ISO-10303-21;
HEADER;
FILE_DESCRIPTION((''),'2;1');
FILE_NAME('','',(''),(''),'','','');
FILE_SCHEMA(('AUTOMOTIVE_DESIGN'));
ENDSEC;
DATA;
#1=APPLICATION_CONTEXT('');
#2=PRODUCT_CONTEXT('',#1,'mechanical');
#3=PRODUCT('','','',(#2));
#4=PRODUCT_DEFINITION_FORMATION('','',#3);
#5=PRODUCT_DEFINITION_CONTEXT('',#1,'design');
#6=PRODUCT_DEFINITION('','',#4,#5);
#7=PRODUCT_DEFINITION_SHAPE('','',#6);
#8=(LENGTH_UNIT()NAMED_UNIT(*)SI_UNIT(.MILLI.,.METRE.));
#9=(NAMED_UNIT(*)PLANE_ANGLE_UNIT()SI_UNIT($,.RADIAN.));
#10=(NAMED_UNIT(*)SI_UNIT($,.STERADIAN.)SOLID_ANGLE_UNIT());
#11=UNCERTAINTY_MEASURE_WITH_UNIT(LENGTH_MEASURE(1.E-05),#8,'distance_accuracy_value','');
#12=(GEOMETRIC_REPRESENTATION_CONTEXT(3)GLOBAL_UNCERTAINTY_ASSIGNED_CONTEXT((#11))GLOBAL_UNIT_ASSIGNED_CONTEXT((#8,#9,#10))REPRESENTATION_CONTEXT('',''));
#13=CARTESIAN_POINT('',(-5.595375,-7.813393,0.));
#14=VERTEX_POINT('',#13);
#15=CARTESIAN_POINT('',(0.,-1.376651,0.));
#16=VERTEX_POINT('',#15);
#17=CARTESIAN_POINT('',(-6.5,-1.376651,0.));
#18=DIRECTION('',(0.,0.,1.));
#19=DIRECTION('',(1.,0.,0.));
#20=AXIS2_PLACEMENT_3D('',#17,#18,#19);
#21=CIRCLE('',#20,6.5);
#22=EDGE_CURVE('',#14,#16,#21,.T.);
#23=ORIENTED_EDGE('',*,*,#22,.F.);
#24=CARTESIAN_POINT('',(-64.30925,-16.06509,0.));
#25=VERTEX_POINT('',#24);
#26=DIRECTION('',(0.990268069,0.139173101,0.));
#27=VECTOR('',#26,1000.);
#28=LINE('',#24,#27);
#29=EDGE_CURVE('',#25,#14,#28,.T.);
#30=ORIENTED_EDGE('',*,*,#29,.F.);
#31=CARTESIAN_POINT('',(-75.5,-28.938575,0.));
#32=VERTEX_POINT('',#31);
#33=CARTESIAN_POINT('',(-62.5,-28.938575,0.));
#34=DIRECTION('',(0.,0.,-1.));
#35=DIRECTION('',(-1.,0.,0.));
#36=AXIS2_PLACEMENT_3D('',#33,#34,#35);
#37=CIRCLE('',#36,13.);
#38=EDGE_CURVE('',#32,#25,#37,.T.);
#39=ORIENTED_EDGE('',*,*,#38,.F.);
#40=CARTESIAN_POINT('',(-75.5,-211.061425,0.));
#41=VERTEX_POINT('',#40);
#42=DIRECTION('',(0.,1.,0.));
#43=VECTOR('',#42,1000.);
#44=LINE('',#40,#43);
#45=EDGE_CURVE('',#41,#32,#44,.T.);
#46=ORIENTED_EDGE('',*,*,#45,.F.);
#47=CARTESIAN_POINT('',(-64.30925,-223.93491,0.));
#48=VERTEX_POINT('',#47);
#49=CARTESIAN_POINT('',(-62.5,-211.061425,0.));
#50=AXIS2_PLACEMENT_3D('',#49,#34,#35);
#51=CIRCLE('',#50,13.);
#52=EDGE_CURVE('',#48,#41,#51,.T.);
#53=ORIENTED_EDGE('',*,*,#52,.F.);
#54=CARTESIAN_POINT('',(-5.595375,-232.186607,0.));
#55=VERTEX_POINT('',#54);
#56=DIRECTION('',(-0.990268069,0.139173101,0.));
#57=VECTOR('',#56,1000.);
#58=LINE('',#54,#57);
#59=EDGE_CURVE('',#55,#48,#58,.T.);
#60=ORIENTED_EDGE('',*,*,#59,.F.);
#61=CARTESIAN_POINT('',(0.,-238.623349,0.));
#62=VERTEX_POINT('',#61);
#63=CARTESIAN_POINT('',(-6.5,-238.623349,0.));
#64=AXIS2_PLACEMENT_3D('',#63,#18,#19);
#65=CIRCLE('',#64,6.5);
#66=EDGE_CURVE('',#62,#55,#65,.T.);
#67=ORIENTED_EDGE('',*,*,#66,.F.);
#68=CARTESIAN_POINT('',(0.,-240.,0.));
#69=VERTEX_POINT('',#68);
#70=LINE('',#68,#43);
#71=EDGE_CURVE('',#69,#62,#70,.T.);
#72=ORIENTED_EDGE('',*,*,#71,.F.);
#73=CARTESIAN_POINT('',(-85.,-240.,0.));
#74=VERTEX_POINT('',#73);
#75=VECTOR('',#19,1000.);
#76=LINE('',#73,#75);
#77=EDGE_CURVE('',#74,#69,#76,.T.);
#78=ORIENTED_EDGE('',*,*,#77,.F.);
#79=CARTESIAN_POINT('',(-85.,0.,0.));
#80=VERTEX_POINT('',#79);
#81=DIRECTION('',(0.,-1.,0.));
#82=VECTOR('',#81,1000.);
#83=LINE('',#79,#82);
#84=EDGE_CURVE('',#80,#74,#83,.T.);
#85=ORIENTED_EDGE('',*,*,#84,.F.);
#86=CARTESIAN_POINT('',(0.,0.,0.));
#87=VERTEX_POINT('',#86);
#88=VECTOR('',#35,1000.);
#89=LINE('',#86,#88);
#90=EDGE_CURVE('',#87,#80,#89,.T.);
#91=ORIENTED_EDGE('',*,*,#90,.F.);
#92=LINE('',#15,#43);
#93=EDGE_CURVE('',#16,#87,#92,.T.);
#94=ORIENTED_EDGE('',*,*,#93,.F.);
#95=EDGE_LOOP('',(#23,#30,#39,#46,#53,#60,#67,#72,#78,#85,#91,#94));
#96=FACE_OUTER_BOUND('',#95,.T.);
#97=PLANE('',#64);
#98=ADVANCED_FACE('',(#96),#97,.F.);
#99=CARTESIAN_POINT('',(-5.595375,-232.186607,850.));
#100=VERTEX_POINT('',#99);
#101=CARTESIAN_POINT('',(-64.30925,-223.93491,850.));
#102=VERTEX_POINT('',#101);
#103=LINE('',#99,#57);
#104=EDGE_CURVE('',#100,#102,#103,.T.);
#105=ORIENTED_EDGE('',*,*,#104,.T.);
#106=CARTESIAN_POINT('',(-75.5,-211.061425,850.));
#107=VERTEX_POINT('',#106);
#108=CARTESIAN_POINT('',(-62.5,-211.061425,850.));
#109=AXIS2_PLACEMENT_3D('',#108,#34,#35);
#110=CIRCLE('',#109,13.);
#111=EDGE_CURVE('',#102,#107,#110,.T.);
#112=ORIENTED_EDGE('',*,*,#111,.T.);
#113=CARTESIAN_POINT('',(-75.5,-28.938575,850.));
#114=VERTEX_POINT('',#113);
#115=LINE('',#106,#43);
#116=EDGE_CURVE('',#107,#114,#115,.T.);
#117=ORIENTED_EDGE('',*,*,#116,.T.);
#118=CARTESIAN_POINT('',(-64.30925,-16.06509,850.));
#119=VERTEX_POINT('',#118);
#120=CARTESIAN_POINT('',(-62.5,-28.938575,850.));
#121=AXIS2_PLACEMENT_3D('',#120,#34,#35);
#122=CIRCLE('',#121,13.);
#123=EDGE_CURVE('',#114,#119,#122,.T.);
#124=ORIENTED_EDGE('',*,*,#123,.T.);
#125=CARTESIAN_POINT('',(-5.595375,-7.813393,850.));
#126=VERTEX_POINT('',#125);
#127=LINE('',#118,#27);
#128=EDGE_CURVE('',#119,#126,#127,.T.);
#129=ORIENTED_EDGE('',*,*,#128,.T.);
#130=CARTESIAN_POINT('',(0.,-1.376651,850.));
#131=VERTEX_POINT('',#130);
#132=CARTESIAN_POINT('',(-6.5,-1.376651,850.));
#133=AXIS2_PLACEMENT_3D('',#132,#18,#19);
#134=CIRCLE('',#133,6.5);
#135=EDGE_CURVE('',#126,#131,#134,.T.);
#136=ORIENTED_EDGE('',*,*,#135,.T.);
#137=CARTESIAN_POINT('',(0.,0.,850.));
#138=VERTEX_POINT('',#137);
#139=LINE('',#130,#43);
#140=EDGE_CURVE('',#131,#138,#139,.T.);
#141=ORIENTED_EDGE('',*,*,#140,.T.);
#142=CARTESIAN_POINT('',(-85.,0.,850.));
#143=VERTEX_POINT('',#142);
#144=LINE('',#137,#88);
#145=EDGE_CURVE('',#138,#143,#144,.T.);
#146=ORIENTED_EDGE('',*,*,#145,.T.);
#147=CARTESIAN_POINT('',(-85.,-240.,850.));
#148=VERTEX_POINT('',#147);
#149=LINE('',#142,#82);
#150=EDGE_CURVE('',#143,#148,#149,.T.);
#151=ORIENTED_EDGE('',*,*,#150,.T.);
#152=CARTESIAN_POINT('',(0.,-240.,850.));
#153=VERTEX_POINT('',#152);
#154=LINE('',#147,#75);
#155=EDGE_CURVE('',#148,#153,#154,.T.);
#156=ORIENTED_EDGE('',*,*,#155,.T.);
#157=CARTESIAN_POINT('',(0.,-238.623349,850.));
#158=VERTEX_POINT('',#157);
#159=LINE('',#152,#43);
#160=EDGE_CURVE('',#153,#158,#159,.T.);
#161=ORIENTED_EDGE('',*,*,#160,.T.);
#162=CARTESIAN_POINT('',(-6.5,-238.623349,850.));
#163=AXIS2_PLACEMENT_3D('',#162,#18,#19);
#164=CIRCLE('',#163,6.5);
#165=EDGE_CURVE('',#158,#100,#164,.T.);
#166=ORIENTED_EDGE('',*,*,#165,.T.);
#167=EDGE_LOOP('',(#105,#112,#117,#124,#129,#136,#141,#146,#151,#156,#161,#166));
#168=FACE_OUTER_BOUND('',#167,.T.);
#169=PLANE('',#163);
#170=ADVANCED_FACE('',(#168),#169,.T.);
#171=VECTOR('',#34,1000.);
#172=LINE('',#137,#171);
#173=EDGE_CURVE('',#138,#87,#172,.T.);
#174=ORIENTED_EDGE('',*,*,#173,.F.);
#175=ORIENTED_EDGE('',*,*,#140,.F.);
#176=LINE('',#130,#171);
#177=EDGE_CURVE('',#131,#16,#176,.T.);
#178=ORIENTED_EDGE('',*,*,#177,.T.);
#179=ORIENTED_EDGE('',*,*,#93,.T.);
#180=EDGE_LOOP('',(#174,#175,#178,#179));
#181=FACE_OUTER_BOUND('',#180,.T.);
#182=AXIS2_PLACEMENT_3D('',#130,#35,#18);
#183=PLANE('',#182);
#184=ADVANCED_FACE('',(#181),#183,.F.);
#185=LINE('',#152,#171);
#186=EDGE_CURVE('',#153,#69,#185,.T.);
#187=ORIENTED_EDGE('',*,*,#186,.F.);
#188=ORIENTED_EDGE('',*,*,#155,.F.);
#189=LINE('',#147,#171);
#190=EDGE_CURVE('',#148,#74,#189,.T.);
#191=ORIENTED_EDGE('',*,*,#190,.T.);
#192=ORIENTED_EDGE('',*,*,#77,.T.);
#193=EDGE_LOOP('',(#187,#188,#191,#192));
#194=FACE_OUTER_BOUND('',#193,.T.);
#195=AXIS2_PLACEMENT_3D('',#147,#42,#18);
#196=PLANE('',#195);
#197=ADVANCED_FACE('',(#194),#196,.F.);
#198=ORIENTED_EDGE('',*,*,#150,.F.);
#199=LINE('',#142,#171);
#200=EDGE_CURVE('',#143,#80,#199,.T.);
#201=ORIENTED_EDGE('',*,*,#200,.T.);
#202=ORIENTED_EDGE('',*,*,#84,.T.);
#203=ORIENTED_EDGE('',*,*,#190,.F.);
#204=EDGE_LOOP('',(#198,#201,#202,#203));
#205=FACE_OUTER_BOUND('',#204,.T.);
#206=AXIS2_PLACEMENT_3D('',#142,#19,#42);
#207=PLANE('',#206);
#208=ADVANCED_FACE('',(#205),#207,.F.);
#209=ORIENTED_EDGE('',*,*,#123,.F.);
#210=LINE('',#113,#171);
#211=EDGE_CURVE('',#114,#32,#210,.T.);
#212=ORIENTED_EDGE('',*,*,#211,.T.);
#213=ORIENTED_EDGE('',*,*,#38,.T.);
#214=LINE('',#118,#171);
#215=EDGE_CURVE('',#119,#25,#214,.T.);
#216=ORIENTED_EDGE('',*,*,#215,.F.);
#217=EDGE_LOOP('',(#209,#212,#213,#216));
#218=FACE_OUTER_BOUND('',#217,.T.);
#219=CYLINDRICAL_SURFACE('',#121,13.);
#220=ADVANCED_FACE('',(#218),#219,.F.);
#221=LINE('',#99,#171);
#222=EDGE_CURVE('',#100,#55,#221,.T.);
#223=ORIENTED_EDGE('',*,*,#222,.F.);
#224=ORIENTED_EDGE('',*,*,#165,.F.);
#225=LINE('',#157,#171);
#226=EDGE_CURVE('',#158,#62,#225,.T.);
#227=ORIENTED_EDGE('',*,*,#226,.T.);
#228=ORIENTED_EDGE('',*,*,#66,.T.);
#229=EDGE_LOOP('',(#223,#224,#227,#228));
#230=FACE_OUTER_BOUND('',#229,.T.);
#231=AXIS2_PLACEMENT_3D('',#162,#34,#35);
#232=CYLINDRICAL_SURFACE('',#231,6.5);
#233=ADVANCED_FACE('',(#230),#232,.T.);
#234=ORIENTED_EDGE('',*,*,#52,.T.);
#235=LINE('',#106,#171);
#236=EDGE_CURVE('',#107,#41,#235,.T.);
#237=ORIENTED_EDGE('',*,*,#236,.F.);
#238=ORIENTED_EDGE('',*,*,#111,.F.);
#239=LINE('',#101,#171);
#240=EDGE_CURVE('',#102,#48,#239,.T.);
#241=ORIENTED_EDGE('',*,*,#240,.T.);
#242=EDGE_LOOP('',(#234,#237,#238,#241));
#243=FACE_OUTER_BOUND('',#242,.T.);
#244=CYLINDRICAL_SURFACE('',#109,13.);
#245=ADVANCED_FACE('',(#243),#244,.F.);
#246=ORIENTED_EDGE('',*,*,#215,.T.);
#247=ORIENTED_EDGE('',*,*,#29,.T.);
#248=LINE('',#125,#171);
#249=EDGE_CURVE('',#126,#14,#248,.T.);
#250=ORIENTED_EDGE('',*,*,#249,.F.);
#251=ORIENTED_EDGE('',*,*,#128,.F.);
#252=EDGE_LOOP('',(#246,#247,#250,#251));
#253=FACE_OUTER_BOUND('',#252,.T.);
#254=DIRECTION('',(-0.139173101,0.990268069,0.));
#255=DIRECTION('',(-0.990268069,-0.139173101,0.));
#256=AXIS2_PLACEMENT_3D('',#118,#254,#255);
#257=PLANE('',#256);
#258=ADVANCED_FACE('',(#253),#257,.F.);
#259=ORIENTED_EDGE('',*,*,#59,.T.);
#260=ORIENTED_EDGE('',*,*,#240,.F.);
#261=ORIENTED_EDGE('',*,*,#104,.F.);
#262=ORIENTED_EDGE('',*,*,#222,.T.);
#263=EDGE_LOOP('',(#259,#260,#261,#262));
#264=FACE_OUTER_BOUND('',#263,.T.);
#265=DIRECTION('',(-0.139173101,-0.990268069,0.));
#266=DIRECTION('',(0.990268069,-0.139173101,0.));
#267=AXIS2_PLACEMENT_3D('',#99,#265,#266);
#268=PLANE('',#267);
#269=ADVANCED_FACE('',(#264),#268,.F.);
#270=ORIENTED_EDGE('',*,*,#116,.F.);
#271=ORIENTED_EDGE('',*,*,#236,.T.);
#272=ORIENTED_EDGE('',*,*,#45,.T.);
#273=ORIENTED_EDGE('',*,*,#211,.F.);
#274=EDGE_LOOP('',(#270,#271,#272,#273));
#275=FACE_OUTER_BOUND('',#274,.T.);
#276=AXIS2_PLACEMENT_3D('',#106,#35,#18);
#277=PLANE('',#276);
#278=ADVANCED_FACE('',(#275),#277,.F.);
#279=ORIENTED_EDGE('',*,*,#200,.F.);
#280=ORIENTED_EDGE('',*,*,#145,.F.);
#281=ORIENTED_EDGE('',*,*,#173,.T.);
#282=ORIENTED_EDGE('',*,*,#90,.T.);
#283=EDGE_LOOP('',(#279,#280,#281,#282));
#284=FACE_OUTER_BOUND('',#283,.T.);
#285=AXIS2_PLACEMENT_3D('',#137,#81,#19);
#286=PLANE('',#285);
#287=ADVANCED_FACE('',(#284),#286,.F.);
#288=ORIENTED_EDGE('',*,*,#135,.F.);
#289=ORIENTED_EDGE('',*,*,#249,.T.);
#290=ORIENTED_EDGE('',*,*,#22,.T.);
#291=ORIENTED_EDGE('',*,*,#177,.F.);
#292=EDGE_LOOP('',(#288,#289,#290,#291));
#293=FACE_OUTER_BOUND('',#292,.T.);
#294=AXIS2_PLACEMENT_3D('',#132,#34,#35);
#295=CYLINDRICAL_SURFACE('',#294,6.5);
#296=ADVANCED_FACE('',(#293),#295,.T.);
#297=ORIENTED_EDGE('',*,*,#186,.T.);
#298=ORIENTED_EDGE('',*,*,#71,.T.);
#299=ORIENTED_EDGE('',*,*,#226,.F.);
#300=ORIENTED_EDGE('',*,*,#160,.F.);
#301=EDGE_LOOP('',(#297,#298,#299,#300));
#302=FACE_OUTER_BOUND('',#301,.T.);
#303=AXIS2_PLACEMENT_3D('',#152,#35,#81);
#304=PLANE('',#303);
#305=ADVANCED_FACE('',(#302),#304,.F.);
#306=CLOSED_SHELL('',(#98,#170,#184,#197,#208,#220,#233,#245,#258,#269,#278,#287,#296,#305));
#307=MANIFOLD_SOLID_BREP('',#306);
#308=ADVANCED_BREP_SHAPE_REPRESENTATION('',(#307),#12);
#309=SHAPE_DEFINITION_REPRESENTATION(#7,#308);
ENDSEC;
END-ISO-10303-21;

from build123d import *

# Parameters (mm, degrees)
EXTRUDE_1_DEPTH = 850


with BuildPart() as part:
    # 草图1 → 凸台-拉伸1 (new body)
    with BuildSketch(Plane.XY):
        with BuildLine():
            Line((0, 0), (-85, 0))
            Line((-85, 0), (-85, -240))
            Line((-85, -240), (0, -240))
            Line((0, -240), (0, -238.623349271))
            ThreePointArc((0, -238.623349271), (-1.594387729, -234.358965582), (-5.595374844, -232.186606824))
            Line((-5.595374844, -232.186606824), (-64.309250312, -223.934909757))
            ThreePointArc((-64.309250312, -223.934909757), (-72.311224543, -219.59019224), (-75.5, -211.061424863))
            Line((-75.5, -211.061424863), (-75.5, -28.938575137))
            ThreePointArc((-75.5, -28.938575137), (-72.311224543, -20.40980776), (-64.309250312, -16.065090243))
            Line((-64.309250312, -16.065090243), (-5.595374844, -7.813393176))
            ThreePointArc((-5.595374844, -7.813393176), (-1.594387729, -5.641034418), (0, -1.376650729))
            Line((0, -1.376650729), (0, 0))
        make_face()
    extrude(amount=EXTRUDE_1_DEPTH)


solid = part.part
